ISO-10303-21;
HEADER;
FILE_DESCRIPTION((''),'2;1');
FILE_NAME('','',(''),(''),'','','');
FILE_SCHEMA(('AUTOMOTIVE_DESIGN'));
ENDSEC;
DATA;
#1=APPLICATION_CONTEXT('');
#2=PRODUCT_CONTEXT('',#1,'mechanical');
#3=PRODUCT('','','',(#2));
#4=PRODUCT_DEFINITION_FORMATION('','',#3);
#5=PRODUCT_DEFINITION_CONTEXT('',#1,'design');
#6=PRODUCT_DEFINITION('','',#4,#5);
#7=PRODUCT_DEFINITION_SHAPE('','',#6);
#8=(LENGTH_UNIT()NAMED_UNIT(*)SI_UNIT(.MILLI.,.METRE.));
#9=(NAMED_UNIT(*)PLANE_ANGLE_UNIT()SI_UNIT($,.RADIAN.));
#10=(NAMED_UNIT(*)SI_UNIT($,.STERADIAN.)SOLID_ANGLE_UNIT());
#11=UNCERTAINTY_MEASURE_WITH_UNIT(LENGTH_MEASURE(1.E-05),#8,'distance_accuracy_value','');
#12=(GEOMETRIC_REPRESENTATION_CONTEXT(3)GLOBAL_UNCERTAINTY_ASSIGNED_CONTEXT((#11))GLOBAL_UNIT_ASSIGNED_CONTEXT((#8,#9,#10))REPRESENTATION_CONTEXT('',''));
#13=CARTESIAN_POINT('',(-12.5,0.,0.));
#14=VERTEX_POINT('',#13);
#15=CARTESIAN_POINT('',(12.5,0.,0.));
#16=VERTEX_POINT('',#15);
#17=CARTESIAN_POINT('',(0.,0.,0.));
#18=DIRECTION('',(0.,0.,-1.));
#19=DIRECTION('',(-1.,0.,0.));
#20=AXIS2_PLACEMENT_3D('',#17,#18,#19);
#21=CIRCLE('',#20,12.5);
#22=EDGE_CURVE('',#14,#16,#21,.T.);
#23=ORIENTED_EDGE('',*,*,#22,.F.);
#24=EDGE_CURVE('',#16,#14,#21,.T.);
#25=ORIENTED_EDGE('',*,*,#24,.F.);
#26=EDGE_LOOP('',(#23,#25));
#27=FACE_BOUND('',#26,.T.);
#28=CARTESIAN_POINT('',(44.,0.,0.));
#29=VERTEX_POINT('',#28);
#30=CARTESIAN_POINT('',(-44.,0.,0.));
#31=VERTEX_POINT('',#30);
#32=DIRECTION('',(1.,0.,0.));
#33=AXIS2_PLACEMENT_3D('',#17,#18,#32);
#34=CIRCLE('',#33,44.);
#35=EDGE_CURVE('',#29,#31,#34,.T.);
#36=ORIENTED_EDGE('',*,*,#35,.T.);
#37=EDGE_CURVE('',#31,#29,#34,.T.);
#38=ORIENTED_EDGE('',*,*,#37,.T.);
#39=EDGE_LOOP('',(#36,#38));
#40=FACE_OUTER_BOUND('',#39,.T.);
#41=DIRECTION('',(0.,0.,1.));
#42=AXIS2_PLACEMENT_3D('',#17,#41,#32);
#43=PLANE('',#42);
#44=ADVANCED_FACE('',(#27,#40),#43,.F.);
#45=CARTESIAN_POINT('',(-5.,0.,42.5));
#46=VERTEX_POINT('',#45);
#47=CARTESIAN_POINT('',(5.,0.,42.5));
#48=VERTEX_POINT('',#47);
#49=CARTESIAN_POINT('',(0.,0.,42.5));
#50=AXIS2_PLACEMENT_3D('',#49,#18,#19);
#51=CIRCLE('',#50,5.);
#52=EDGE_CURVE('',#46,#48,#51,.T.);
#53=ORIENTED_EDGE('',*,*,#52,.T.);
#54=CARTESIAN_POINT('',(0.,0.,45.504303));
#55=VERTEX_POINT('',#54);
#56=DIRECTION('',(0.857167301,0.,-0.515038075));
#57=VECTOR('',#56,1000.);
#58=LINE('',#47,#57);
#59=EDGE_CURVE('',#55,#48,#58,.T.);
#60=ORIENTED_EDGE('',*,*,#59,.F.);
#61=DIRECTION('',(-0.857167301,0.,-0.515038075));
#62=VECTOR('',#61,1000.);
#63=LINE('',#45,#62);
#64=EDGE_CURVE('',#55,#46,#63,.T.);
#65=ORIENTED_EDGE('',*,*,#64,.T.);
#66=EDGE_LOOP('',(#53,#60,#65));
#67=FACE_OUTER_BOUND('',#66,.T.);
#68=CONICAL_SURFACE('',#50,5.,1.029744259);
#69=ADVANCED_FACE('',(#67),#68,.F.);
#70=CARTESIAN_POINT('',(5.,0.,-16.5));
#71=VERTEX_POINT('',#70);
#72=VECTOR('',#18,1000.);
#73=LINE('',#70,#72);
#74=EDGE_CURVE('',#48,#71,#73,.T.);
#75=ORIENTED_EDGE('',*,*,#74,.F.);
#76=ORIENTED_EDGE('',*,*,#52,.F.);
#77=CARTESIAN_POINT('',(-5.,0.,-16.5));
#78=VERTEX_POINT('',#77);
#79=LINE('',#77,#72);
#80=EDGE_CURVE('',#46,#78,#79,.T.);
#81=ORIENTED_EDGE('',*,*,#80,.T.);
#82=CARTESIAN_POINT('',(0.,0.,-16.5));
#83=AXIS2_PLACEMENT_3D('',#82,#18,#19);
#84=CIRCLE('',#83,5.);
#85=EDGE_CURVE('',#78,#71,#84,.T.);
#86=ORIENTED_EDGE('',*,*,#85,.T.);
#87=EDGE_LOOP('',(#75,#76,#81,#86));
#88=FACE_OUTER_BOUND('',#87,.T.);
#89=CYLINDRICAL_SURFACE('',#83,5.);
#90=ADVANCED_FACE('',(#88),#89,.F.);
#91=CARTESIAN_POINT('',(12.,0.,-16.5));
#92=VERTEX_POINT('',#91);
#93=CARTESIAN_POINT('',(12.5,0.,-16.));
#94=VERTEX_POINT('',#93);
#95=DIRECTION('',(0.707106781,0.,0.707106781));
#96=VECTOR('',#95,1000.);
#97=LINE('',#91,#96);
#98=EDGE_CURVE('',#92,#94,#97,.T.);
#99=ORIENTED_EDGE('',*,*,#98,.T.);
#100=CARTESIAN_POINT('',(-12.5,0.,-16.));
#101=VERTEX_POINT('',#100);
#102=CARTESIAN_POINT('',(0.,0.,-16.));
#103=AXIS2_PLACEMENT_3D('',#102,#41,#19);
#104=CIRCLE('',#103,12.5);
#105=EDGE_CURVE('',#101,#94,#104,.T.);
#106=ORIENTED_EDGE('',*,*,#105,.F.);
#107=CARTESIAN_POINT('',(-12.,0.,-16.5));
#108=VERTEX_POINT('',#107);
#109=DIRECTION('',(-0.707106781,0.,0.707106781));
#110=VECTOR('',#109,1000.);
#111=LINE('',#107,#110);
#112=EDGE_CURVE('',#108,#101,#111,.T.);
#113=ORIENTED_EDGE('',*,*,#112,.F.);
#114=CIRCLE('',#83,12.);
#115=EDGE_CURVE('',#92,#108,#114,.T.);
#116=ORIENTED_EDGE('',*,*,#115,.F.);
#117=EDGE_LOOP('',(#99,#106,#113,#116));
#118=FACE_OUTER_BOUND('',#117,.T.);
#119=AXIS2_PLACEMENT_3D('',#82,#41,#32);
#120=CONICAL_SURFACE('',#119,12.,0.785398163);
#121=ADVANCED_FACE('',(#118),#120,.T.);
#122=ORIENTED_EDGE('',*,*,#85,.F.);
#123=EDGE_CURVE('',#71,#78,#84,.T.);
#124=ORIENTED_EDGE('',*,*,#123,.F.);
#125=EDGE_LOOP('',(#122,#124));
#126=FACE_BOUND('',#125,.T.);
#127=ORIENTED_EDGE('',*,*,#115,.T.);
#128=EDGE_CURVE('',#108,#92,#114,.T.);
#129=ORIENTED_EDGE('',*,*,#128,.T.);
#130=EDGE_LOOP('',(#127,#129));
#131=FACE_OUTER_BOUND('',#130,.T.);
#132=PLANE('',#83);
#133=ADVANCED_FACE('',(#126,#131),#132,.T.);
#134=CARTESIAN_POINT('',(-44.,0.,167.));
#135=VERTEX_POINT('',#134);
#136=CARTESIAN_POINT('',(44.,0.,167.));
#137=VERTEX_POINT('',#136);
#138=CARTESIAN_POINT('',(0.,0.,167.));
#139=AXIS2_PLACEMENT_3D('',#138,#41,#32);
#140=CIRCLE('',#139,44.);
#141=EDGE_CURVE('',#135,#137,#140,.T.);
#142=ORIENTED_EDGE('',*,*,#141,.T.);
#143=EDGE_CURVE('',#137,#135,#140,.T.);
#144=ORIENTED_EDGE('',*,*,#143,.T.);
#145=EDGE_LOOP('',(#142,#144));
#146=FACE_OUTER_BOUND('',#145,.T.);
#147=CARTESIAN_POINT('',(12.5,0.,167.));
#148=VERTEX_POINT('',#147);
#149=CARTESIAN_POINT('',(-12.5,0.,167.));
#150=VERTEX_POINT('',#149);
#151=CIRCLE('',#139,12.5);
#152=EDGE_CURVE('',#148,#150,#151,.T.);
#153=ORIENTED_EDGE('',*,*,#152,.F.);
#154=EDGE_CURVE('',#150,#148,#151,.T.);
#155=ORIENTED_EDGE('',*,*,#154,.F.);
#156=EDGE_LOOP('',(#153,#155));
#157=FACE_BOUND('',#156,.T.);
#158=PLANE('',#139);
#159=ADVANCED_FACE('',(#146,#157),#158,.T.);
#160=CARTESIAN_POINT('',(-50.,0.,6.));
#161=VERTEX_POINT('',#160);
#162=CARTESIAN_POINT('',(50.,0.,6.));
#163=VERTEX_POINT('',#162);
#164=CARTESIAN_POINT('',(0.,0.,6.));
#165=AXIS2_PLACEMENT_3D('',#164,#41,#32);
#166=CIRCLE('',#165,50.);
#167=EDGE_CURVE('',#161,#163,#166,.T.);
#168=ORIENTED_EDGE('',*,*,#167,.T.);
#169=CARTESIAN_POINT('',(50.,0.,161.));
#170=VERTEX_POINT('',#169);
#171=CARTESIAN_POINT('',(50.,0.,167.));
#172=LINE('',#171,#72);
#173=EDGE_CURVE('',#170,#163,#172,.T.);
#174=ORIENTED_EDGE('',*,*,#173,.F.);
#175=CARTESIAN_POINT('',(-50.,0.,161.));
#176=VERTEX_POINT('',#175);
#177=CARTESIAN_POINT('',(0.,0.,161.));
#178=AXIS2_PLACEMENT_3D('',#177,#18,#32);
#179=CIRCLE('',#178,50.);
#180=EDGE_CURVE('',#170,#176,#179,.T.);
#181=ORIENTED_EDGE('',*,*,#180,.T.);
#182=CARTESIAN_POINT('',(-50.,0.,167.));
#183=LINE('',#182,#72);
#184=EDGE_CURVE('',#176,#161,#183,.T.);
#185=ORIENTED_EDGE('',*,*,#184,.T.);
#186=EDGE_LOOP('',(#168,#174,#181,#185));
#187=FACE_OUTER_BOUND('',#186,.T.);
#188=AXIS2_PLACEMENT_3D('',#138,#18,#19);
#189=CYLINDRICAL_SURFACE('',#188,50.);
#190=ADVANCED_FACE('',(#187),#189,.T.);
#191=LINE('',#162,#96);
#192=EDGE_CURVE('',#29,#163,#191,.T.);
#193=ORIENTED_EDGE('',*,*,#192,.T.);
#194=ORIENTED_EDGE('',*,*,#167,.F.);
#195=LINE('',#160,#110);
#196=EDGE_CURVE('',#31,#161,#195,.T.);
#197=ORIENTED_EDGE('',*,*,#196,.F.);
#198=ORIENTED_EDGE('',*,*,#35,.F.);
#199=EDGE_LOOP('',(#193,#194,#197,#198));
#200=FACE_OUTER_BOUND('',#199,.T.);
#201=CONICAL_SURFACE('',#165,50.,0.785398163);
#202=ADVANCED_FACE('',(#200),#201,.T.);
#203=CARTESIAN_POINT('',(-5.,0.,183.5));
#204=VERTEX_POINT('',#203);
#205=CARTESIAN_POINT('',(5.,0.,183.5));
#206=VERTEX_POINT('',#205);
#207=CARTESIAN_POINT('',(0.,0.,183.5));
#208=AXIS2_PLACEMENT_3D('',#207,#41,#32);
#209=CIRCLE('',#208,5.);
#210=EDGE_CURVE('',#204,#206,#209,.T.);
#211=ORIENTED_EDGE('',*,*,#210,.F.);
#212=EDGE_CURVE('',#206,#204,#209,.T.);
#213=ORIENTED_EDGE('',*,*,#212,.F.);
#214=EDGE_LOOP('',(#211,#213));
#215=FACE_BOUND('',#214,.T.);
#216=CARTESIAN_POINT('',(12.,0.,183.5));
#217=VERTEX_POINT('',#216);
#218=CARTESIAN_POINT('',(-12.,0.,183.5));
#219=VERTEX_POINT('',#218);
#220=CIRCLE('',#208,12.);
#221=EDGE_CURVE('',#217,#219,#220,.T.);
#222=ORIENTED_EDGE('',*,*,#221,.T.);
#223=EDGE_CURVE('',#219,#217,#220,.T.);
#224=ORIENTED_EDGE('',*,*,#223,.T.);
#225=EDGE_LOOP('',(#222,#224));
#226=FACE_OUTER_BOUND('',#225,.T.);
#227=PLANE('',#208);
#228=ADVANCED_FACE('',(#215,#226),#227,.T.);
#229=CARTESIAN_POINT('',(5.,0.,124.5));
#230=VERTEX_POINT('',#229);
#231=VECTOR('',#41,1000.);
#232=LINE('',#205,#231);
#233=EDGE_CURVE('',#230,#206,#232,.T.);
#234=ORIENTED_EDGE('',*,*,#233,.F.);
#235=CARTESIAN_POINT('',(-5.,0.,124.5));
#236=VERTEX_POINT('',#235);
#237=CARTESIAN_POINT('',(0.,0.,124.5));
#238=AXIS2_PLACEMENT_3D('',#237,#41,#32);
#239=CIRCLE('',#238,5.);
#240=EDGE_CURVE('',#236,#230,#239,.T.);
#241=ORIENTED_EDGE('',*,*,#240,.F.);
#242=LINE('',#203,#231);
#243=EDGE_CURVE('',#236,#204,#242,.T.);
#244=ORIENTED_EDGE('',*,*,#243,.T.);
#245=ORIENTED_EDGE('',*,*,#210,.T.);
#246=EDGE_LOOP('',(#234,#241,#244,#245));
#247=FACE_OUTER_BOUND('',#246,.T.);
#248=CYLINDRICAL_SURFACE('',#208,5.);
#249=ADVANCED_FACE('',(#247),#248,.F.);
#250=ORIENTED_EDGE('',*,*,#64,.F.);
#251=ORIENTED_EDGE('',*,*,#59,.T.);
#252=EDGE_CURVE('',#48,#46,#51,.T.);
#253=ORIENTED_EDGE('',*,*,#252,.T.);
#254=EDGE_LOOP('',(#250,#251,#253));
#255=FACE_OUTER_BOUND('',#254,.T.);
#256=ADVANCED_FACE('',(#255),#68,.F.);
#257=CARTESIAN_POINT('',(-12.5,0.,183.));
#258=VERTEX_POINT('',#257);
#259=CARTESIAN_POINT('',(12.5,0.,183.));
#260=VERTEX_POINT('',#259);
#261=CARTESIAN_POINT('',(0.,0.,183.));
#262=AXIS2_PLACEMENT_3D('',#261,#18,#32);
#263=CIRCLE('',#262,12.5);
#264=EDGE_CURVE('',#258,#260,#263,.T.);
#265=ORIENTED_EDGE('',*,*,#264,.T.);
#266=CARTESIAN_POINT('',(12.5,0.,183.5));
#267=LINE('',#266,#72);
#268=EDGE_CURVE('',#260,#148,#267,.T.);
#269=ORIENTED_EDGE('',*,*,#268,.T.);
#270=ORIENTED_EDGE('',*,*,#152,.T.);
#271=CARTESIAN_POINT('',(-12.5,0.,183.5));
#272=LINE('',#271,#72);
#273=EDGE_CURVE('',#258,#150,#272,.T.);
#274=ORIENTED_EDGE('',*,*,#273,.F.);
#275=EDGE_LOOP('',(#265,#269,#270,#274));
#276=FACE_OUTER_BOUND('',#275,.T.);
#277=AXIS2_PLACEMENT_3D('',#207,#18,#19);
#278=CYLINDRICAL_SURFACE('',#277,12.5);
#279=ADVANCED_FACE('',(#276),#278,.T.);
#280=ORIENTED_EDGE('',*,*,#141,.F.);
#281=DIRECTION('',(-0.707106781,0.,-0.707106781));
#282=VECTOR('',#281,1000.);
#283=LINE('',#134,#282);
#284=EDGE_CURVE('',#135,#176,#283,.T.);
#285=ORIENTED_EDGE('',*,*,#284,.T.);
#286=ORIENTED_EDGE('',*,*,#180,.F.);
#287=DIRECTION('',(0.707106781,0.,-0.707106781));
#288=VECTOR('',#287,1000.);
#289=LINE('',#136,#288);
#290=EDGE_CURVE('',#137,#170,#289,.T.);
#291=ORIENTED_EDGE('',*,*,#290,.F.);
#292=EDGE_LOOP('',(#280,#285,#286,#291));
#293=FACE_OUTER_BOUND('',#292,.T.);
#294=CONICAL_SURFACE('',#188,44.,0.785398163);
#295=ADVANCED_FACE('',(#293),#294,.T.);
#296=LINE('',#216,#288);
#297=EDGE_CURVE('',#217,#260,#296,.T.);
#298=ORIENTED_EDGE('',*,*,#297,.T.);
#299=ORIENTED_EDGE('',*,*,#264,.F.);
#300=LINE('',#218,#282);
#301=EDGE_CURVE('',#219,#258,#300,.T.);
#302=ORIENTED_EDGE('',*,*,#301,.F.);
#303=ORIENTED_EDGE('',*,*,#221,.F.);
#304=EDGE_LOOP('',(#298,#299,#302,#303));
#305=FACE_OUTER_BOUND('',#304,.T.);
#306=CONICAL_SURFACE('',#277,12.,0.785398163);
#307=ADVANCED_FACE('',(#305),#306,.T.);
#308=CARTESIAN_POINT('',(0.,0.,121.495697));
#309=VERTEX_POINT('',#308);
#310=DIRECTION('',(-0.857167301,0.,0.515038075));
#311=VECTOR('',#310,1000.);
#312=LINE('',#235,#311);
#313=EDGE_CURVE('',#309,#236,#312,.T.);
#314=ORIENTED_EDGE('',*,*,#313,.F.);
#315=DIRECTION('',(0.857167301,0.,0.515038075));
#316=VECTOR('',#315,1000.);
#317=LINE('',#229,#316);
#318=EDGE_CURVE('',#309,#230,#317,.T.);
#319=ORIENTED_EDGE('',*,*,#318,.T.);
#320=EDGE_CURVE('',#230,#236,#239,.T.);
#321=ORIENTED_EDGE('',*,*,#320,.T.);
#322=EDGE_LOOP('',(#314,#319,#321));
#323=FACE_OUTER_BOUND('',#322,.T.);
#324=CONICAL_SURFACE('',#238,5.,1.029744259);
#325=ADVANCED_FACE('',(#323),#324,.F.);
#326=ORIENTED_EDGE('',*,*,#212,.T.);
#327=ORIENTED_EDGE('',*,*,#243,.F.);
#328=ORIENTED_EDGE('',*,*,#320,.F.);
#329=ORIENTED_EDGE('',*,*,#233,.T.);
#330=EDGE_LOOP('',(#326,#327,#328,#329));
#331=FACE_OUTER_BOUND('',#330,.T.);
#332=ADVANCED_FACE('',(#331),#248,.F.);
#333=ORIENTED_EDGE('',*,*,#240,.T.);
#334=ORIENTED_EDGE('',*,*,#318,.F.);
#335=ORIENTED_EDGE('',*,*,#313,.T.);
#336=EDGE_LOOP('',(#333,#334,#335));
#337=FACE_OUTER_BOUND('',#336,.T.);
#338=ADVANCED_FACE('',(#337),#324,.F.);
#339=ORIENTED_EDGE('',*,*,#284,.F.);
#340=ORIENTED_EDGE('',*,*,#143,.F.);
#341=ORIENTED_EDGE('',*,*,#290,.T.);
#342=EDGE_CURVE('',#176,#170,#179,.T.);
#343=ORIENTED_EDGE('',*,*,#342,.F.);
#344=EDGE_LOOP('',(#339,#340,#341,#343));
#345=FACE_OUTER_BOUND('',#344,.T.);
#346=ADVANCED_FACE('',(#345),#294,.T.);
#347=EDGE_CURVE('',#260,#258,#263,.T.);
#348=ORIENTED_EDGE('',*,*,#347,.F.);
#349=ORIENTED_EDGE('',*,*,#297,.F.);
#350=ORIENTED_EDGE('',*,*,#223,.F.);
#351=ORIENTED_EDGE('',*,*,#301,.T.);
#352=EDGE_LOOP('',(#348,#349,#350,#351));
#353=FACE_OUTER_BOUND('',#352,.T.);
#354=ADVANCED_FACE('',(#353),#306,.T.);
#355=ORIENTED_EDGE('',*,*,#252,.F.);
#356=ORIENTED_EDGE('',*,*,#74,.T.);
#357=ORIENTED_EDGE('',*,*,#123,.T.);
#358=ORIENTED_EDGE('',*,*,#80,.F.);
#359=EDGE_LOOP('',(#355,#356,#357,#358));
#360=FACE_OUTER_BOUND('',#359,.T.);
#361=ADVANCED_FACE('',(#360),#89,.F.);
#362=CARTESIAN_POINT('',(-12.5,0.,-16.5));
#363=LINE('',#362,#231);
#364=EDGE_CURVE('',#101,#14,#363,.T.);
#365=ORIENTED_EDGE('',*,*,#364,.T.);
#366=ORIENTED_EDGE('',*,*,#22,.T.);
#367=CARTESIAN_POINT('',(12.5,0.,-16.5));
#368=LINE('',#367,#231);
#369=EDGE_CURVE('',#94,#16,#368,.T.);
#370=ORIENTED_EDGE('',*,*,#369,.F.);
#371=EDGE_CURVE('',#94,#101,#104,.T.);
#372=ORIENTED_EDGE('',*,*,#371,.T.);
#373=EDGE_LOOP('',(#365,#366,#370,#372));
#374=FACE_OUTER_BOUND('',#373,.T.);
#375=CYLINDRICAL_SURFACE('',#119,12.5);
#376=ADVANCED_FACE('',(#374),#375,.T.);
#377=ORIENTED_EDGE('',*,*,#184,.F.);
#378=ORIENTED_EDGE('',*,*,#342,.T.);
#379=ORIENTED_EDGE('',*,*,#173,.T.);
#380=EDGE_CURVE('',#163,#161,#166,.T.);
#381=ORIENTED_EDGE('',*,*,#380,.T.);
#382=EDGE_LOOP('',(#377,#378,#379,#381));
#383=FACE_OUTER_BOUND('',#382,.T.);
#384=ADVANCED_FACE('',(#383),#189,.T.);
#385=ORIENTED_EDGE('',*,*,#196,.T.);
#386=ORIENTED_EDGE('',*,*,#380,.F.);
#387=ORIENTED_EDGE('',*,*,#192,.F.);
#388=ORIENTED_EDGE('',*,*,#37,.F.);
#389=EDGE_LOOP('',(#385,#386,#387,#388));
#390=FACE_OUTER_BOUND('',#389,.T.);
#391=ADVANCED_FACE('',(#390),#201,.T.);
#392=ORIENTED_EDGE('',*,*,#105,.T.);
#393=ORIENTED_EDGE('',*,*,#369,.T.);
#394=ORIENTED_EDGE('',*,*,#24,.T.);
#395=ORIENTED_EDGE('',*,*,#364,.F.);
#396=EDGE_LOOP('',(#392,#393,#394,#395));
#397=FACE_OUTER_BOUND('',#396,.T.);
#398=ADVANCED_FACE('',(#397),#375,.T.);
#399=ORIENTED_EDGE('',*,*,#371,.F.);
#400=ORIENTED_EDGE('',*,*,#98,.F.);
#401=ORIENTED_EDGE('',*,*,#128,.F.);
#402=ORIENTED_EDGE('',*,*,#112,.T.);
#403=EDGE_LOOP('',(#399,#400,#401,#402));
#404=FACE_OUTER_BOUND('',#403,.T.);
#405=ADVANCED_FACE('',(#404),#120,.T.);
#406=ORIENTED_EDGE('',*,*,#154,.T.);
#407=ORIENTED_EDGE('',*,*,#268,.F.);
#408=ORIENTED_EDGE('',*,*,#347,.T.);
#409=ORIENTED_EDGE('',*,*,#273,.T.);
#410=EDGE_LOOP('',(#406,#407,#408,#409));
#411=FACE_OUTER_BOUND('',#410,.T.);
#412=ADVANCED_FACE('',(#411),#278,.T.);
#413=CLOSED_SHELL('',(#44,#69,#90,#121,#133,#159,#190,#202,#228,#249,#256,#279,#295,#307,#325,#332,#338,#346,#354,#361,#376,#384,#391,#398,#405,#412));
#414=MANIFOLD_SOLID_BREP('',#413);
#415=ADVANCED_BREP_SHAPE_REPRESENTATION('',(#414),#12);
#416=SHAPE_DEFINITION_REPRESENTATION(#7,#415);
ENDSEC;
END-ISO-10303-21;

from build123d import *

# Parameters (mm, degrees)
BODY_PROFILE_100_R              = 50
MAIN_BODY_100X167_DEPTH         = 167
SPIGOT_1_PROFILE_25_R           = 12.5
END_SPIGOT_1_25X16_5_DEPTH      = 16.5
END_START                       = 16.5
SPIGOT_2_PROFILE_25_R           = 12.5
END_SPIGOT_2_25X16_5_DEPTH      = 16.5
SPIGOT_2_DOWEL_HOLE_10X59_D     = 10
SPIGOT_2_DOWEL_HOLE_10X59_DEPTH = 59
SPIGOT_2_DOWEL_HOLE_10X59_TIP   = 3.004303095
SPIGOT_1_DOWEL_HOLE_10X59_D     = 10
SPIGOT_1_DOWEL_HOLE_10X59_DEPTH = 59
SPIGOT_1_DOWEL_HOLE_10X59_TIP   = 3.004303095
SPIGOT_EDGE_CHAMFER_0_5_SIZE    = 0.5
BODY_EDGE_CHAMFER_6_SIZE        = 6


with BuildPart() as part:
    # Body Profile Ø100 → Main Body Ø100x167 (new body)
    with BuildSketch(Plane.XY):
        with Locations(Location((0, 0, 0), (0, 0, 180))):
            Circle(BODY_PROFILE_100_R)
    extrude(amount=MAIN_BODY_100X167_DEPTH)

    # Spigot 1 Profile Ø25 → End Spigot 1 Ø25x16.5 (add)
    with BuildSketch(Plane.XY.offset(167)):
        Circle(SPIGOT_1_PROFILE_25_R)
    extrude(amount=END_SPIGOT_1_25X16_5_DEPTH)

    # Spigot 2 Profile Ø25 → End Spigot 2 Ø25x16.5 (add)
    with BuildSketch(Plane(origin=(0, 0, 0), x_dir=(-1, 0, 0), z_dir=(0, 0, -1)).offset(END_START)):
        with Locations(Location((0, 0, 0), (0, 0, 180))):
            Circle(SPIGOT_2_PROFILE_25_R)
    extrude(amount=-END_SPIGOT_2_25X16_5_DEPTH)

    # Spigot 2 Dowel Hole Ø10x59
    with Locations(Plane(origin=(0, 0, -16.5), x_dir=(-1, 0, 0), z_dir=(0, 0, -1))):
        with Locations((0, 0)):
            Hole(SPIGOT_2_DOWEL_HOLE_10X59_D / 2, depth=SPIGOT_2_DOWEL_HOLE_10X59_DEPTH)
            with Locations((0, 0, -(SPIGOT_2_DOWEL_HOLE_10X59_DEPTH + SPIGOT_2_DOWEL_HOLE_10X59_TIP / 2))):  # 118° drill point
                Cone(0, SPIGOT_2_DOWEL_HOLE_10X59_D / 2, SPIGOT_2_DOWEL_HOLE_10X59_TIP, mode=Mode.SUBTRACT)

    # Spigot 1 Dowel Hole Ø10x59
    with Locations(Plane.XY.offset(183.5)):
        with Locations((0, 0)):
            Hole(SPIGOT_1_DOWEL_HOLE_10X59_D / 2, depth=SPIGOT_1_DOWEL_HOLE_10X59_DEPTH)
            with Locations((0, 0, -(SPIGOT_1_DOWEL_HOLE_10X59_DEPTH + SPIGOT_1_DOWEL_HOLE_10X59_TIP / 2))):  # 118° drill point
                Cone(0, SPIGOT_1_DOWEL_HOLE_10X59_D / 2, SPIGOT_1_DOWEL_HOLE_10X59_TIP, mode=Mode.SUBTRACT)

    # Spigot Edge Chamfer 0.5
    spigot_edge_chamfer_0_5_edges = [part.edges().sort_by_distance(p)[0] for p in [
        (-12.5, 0, -16.5),
        (-12.5, 0, 183.5),
    ]]
    chamfer(spigot_edge_chamfer_0_5_edges, length=SPIGOT_EDGE_CHAMFER_0_5_SIZE)

    # Body Edge Chamfer 6
    body_edge_chamfer_6_edges = [part.edges().sort_by_distance(p)[0] for p in [
        (50, 0, 0),
        (50, 0, 167),
    ]]
    chamfer(body_edge_chamfer_6_edges, length=BODY_EDGE_CHAMFER_6_SIZE)


solid = part.part
